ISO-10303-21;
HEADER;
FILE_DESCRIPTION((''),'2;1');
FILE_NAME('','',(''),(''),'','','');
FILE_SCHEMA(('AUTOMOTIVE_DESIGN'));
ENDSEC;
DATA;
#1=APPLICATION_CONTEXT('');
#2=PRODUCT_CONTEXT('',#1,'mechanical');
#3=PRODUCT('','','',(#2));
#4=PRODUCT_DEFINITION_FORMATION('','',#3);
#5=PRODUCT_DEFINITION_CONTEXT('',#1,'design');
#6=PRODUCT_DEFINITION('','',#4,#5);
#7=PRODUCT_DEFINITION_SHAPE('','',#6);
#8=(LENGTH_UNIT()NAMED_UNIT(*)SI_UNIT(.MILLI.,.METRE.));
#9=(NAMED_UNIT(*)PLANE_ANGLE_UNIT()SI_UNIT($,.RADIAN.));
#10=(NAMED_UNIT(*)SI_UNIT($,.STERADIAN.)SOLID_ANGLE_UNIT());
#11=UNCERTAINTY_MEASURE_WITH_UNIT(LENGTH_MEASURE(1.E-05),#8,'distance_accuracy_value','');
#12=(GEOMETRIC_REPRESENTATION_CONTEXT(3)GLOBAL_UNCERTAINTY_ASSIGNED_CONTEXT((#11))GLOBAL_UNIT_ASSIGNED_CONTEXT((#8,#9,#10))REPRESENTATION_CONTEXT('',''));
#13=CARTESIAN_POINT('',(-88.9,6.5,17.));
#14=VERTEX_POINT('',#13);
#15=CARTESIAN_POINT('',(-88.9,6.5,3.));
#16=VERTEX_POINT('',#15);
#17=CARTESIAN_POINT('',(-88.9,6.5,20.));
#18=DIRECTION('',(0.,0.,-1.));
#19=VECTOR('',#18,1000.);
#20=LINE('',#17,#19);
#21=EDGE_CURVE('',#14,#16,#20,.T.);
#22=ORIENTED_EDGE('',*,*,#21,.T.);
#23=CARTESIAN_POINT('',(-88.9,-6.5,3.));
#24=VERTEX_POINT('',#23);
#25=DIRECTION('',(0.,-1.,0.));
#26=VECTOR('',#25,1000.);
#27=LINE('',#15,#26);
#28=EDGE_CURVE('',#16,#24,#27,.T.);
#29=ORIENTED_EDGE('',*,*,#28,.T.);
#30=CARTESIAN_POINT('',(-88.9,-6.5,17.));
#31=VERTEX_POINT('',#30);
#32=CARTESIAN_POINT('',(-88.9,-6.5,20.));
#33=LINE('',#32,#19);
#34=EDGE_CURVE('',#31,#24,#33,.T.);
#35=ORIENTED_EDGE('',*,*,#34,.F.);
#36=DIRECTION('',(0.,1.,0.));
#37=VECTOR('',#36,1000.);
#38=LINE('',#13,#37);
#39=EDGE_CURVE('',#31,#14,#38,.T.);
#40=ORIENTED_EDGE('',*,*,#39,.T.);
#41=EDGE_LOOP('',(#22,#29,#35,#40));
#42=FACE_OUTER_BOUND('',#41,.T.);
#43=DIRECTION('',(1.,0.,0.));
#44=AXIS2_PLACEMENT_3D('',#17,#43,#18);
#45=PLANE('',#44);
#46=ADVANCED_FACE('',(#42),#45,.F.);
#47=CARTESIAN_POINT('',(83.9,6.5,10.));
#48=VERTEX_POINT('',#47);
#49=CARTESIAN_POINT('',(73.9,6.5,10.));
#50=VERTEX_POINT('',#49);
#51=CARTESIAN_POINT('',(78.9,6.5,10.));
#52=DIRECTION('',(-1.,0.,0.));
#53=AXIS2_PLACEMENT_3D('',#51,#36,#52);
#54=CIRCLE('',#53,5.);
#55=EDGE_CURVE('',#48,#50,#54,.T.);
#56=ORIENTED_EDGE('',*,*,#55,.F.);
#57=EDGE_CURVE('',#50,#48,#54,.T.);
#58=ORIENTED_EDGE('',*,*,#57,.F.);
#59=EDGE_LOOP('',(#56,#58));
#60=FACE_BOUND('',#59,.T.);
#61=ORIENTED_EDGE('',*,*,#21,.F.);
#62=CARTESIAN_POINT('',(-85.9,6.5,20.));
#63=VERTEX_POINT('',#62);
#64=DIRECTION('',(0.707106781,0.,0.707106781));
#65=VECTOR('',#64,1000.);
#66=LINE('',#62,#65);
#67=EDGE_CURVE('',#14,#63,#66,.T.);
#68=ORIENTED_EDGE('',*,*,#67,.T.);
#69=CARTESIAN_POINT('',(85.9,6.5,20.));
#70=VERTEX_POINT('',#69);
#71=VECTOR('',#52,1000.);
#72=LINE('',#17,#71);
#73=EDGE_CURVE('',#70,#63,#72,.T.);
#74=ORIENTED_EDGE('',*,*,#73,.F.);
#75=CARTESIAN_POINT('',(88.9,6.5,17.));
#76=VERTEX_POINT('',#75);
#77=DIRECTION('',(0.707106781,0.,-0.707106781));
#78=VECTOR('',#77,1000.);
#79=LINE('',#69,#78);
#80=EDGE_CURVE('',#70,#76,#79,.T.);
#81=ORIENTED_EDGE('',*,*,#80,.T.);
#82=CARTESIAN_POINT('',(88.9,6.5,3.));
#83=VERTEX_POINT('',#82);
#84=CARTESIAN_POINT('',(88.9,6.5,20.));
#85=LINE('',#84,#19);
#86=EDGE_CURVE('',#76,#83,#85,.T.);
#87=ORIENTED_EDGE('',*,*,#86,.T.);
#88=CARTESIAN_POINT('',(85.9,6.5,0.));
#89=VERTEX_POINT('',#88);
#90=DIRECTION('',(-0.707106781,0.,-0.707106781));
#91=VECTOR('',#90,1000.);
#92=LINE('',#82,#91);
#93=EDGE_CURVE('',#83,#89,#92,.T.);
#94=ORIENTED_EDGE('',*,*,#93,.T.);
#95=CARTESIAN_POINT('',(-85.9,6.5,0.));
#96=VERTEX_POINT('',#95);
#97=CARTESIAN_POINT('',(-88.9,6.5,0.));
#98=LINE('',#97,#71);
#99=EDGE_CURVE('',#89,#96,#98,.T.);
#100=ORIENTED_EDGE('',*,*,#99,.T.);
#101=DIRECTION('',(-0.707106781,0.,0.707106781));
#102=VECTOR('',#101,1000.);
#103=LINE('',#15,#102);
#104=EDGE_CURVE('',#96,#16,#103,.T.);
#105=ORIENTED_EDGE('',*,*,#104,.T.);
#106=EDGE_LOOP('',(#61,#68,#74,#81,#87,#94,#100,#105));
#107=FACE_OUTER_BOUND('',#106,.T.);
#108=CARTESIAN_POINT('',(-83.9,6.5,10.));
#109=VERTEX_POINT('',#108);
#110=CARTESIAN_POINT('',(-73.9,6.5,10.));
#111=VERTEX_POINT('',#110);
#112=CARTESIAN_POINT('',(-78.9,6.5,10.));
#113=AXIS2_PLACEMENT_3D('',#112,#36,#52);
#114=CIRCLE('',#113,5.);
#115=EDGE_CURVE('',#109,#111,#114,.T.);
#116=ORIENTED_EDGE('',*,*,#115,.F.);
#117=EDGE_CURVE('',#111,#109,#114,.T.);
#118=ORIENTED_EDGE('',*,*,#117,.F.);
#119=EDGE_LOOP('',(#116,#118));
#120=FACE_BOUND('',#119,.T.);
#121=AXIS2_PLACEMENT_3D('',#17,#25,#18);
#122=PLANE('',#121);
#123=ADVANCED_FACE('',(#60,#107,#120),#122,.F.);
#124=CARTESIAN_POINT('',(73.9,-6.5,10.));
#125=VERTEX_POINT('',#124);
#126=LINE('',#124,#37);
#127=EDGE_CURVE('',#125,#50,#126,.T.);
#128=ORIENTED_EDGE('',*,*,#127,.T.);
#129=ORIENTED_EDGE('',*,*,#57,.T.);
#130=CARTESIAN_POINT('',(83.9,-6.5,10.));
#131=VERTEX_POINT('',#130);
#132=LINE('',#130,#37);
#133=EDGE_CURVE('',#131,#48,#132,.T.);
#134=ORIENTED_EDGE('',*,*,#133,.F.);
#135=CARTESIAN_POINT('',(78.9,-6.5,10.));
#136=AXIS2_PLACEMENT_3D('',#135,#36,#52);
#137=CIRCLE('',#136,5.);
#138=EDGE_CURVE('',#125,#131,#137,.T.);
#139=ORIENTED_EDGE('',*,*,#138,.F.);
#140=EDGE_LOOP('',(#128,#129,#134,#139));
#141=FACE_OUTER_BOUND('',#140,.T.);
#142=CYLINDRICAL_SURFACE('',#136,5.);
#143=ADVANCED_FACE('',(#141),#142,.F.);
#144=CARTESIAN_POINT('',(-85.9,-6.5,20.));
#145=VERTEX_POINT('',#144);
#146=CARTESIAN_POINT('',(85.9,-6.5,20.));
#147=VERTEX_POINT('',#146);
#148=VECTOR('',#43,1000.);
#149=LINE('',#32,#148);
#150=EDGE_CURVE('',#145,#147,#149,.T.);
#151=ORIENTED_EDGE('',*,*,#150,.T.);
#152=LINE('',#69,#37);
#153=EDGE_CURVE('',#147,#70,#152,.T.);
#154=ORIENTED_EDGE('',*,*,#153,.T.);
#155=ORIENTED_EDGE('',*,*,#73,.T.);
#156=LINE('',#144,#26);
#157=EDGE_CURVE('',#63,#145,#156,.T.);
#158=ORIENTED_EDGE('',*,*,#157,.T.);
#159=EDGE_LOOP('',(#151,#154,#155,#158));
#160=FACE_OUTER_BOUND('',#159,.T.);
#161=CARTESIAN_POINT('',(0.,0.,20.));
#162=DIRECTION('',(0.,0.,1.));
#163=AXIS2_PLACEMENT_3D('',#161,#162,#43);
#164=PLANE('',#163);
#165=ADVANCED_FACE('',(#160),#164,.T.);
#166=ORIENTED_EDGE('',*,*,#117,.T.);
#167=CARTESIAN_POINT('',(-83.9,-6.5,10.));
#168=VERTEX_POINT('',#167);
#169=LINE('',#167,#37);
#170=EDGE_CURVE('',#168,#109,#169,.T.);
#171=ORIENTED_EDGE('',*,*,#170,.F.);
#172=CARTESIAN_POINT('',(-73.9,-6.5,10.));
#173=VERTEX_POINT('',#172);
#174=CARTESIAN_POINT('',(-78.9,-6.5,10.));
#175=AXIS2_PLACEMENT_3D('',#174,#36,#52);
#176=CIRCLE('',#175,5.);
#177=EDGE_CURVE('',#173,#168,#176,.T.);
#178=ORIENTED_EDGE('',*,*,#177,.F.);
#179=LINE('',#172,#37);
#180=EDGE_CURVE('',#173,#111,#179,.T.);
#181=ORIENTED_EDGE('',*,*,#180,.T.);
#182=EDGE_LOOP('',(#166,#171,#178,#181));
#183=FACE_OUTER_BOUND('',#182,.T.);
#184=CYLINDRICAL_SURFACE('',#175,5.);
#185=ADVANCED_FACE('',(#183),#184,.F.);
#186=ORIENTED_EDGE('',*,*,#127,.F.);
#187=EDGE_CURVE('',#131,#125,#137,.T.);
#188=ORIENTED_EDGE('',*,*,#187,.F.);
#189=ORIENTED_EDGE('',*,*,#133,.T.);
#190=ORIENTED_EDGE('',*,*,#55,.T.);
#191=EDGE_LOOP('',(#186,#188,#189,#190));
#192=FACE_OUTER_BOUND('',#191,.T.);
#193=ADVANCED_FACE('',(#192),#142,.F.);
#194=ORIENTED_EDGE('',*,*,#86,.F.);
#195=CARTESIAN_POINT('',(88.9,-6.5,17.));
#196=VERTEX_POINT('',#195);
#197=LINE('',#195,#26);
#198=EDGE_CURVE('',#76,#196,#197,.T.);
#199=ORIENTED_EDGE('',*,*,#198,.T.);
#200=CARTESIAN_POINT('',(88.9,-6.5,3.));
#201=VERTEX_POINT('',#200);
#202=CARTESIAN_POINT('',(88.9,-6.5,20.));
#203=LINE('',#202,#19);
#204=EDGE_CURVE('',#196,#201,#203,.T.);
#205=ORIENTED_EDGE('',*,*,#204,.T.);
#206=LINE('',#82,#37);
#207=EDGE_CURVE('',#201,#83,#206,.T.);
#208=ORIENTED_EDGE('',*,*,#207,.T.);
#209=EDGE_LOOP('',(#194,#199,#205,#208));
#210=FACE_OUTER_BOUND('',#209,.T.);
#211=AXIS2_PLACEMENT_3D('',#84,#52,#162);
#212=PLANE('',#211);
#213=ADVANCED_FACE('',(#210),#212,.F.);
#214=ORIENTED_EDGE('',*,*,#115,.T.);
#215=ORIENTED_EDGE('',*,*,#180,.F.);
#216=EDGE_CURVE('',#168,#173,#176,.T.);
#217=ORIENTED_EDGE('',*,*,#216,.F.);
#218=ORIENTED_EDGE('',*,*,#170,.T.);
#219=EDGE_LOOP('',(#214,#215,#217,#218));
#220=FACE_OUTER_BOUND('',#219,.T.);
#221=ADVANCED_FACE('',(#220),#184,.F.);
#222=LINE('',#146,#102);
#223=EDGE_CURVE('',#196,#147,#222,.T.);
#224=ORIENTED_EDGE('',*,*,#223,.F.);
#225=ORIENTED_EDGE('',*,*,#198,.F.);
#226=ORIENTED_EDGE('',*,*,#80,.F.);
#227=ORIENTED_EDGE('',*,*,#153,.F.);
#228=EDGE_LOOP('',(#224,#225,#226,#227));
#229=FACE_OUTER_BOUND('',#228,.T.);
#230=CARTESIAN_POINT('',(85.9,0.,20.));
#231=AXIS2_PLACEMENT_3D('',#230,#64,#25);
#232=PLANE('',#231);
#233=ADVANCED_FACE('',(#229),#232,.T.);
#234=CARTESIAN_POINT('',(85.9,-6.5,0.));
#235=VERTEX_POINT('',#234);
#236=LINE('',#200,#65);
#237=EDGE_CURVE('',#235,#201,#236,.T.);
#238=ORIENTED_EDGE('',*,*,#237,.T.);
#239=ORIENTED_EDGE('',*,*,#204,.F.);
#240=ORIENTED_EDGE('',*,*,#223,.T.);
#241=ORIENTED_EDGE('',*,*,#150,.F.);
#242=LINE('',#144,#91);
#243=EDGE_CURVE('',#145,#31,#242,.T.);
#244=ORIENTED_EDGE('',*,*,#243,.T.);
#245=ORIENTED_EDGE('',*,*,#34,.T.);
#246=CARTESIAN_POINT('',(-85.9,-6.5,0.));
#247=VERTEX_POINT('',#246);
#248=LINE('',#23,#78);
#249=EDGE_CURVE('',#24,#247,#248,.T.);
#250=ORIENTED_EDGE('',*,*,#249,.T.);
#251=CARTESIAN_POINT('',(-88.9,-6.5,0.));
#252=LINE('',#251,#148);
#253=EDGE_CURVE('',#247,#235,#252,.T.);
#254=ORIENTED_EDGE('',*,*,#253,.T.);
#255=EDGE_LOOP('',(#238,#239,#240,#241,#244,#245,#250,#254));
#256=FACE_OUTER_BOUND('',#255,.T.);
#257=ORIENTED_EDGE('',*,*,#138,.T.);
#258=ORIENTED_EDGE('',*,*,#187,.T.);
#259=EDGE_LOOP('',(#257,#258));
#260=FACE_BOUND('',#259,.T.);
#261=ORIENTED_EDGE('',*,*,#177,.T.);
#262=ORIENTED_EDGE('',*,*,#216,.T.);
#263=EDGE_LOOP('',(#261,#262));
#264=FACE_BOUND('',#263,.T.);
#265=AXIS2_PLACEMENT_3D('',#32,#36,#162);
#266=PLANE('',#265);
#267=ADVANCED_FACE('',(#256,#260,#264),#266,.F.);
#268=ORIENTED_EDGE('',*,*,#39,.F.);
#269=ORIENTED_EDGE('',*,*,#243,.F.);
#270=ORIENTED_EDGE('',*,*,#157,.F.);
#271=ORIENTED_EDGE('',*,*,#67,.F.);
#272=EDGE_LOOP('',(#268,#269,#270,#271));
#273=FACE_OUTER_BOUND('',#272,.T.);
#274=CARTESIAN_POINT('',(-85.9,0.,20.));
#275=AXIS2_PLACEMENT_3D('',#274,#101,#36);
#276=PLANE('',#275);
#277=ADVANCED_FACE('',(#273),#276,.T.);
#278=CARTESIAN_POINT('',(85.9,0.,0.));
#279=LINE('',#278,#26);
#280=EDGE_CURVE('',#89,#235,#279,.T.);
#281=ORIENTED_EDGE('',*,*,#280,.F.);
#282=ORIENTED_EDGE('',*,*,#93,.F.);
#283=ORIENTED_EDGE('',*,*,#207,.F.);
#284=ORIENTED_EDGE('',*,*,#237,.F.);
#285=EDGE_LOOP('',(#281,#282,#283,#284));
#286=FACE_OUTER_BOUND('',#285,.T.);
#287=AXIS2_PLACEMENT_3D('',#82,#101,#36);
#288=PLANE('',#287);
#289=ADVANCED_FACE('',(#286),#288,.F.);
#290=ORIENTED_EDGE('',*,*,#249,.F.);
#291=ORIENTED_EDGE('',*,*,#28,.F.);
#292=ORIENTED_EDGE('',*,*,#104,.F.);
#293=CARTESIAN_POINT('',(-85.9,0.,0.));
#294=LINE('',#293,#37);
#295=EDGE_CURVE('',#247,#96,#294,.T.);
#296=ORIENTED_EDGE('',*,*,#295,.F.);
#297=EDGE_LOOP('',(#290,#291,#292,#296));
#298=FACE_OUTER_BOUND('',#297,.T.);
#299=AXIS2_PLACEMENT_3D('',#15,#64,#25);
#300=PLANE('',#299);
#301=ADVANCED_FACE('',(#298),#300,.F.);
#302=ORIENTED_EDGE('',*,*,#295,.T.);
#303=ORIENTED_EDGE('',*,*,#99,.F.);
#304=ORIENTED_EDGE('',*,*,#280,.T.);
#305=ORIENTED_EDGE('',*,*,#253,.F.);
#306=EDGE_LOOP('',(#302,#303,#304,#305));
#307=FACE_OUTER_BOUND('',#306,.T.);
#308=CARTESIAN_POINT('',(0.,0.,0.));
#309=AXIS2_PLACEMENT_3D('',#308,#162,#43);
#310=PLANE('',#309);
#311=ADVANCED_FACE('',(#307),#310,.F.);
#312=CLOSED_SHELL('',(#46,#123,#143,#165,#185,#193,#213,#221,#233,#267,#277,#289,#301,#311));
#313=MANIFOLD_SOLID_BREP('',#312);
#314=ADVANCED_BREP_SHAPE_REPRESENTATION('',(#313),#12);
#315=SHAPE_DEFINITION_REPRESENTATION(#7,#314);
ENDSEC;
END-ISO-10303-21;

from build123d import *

# Parameters (mm, degrees)
SKETCH1_W           = 177.8
SKETCH1_H           = 13
BOSS_EXTRUDE1_DEPTH = 20
CHAMFER1_SIZE       = 3
SKETCH2_R           = 5
CUT_EXTRUDE1_DEPTH  = 13
LPATTERN1_COUNT     = 2
LPATTERN1_PITCH     = 157.8


with BuildPart() as part:
    # Sketch1 → Boss-Extrude1 (new body)
    with BuildSketch(Plane.XY):
        Rectangle(SKETCH1_W, SKETCH1_H)
    extrude(amount=BOSS_EXTRUDE1_DEPTH)

    # Chamfer1
    chamfer1_edges = [part.edges().sort_by_distance(p)[0] for p in [
        (-88.9, 0, 20),
        (88.9, 0, 20),
        (-88.9, 0, 0),
        (88.9, 0, 0),
    ]]
    chamfer(chamfer1_edges, length=CHAMFER1_SIZE)

    # Sketch2 → Cut-Extrude1 (cut)
    with BuildSketch(Plane(origin=(0, 6.5, 0), x_dir=(1, 0, 0), z_dir=(0, 1, 0))):
        with Locations(Location((-78.9, -10, 0), (0, 0, 180))):
            Circle(SKETCH2_R)
    cut_extrude1 = extrude(amount=-CUT_EXTRUDE1_DEPTH, mode=Mode.SUBTRACT)

    # LPattern1: Cut-Extrude1 ×2
    with Locations(*[(i * LPATTERN1_PITCH, 0, 0) for i in range(1, LPATTERN1_COUNT)]):
        add(cut_extrude1, mode=Mode.SUBTRACT)


solid = part.part
